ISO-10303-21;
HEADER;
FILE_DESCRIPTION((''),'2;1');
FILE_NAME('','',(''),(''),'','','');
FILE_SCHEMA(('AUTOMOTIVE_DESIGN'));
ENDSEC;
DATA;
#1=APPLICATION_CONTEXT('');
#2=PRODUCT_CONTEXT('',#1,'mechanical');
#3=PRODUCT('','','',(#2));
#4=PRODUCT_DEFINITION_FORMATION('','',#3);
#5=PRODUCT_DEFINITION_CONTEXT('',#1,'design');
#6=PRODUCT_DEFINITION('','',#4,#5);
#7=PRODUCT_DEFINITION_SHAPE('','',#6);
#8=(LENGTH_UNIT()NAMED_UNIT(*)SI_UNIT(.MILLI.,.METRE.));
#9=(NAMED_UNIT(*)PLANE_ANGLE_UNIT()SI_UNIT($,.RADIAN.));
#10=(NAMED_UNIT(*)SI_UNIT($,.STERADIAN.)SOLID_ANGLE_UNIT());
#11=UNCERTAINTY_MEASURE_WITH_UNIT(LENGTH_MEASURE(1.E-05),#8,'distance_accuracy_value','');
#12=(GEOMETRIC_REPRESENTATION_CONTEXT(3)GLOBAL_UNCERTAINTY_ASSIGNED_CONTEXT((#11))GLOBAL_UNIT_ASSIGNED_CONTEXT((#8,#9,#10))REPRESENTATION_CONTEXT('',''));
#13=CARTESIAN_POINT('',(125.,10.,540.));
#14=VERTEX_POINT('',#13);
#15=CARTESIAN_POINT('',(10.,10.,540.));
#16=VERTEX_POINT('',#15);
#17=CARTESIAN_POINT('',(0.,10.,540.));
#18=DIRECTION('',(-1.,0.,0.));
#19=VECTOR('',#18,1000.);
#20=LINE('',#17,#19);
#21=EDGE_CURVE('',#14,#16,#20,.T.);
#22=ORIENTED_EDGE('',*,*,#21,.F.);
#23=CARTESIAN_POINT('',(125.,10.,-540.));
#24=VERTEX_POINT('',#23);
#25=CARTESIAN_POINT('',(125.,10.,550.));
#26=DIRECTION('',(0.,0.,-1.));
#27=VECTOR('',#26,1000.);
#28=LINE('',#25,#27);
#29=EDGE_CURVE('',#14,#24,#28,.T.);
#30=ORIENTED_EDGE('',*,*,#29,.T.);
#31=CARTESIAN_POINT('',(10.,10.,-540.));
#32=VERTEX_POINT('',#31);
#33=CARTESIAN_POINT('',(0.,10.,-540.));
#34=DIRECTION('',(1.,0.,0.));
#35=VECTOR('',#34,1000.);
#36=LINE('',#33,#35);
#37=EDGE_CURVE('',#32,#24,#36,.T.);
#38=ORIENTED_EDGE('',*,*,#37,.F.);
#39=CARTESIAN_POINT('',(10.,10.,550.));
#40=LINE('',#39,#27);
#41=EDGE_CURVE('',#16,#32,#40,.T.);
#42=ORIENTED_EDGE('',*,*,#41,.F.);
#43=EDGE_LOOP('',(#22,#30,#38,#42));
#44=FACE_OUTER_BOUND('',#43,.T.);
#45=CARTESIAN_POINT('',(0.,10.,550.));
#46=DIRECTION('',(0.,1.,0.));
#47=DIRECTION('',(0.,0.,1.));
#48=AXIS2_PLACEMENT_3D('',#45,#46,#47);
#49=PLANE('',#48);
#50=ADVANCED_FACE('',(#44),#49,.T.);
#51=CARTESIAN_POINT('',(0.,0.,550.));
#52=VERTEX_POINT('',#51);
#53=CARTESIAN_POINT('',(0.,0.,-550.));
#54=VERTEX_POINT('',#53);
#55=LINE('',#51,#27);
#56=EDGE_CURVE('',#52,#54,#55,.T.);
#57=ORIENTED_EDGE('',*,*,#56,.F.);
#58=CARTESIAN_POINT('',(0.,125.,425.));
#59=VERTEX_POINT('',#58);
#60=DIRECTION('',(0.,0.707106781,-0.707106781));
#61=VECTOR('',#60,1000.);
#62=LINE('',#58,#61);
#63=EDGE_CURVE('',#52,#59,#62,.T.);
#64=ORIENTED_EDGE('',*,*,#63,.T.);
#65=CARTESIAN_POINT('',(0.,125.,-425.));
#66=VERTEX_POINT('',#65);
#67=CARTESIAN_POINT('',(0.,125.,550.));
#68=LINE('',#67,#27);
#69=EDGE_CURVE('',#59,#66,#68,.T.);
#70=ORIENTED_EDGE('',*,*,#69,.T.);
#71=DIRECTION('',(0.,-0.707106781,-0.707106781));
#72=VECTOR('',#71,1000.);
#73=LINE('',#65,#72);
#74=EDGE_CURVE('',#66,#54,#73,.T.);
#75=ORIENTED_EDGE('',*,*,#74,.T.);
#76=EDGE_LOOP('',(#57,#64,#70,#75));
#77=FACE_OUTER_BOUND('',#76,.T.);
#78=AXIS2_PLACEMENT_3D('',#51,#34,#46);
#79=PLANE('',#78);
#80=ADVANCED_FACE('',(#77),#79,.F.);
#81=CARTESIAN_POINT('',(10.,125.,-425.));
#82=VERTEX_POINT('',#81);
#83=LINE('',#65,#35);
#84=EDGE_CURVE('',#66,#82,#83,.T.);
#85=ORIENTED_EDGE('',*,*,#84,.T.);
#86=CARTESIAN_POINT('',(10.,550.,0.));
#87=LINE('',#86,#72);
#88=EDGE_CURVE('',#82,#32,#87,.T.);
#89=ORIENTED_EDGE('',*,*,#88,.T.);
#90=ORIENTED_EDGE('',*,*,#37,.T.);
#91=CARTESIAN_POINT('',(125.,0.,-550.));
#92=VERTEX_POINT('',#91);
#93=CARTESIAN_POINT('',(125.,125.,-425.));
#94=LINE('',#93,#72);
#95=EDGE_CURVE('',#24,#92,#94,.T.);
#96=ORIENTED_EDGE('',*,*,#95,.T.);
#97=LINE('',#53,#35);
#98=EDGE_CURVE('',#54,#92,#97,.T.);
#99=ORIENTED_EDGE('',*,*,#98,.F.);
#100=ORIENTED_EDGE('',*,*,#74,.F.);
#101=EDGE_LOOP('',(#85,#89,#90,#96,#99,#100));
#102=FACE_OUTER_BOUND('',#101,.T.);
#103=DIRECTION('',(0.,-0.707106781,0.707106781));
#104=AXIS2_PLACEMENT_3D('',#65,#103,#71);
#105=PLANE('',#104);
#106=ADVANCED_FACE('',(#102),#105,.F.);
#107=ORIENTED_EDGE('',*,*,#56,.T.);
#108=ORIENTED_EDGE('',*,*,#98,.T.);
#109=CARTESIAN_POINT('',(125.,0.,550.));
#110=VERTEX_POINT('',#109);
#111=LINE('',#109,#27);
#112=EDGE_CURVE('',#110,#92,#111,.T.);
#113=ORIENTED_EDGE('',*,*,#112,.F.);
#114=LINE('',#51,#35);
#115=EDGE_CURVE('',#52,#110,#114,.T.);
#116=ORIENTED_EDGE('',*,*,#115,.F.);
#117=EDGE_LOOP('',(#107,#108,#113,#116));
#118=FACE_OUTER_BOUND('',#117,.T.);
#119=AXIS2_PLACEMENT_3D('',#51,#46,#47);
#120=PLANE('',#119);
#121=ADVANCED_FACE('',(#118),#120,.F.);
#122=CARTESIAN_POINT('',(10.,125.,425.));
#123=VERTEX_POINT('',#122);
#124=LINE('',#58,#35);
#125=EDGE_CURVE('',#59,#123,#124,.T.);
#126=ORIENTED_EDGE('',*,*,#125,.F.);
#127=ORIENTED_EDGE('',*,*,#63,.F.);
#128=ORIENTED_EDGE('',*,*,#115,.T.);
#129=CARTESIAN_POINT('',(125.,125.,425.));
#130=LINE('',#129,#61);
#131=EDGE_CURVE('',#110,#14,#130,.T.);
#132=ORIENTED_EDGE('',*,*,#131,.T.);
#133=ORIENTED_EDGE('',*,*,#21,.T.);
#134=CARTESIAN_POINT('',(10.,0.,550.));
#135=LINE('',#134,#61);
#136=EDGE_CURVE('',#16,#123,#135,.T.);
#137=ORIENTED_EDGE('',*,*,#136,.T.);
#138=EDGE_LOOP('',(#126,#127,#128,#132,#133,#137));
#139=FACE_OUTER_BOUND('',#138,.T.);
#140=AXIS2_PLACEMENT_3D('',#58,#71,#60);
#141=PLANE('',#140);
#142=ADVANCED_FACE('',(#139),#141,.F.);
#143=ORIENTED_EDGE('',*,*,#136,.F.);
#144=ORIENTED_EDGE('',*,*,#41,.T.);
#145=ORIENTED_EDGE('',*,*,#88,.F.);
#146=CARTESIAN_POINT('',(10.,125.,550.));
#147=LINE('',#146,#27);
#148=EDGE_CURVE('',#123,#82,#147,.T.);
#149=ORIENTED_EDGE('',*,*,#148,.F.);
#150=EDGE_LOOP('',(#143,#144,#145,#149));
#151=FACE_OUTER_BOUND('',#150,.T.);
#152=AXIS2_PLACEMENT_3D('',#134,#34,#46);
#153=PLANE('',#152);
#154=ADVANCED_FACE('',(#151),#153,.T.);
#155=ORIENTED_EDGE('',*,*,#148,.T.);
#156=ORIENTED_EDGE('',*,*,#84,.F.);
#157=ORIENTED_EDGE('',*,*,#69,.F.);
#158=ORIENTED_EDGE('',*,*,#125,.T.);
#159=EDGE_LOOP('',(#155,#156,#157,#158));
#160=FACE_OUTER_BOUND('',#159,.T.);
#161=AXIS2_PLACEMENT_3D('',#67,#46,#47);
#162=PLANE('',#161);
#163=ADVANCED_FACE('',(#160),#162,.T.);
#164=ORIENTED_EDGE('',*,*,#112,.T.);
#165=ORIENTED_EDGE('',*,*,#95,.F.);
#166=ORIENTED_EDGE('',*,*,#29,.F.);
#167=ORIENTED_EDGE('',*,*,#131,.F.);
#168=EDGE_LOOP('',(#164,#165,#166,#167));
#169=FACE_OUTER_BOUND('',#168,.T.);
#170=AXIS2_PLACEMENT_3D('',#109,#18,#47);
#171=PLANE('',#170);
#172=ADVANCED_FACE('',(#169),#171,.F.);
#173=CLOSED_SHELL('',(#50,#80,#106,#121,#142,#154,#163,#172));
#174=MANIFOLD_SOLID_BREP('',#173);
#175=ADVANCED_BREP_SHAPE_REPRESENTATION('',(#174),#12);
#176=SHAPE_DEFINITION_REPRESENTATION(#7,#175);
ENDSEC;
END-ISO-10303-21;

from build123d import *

# Parameters (mm, degrees)
EXTRUDE_1_DEPTH     = 550
CUT_EXTRUDE_1_DEPTH = 578.711000415


with BuildPart() as part:
    # 草图1 → 凸台-拉伸1 (new, symmetric)
    with BuildSketch(Plane.XY):
        Polygon((0, 125), (10, 125), (10, 10), (125, 10), (125, 0), (0, 0), align=None)
    extrude(amount=EXTRUDE_1_DEPTH, both=True)

    # 草图2 → 切除-拉伸1 (cut, through all)
    with BuildSketch(Plane(origin=(125, 0, 0), x_dir=(0, 0, -1), z_dir=(1, 0, 0))):
        Polygon((-550, 0), (-550, 125), (-425, 125), align=None)
        Polygon((425, 125), (550, 0), (550, 125), align=None)
    extrude(amount=-CUT_EXTRUDE_1_DEPTH, mode=Mode.SUBTRACT)


solid = part.part
